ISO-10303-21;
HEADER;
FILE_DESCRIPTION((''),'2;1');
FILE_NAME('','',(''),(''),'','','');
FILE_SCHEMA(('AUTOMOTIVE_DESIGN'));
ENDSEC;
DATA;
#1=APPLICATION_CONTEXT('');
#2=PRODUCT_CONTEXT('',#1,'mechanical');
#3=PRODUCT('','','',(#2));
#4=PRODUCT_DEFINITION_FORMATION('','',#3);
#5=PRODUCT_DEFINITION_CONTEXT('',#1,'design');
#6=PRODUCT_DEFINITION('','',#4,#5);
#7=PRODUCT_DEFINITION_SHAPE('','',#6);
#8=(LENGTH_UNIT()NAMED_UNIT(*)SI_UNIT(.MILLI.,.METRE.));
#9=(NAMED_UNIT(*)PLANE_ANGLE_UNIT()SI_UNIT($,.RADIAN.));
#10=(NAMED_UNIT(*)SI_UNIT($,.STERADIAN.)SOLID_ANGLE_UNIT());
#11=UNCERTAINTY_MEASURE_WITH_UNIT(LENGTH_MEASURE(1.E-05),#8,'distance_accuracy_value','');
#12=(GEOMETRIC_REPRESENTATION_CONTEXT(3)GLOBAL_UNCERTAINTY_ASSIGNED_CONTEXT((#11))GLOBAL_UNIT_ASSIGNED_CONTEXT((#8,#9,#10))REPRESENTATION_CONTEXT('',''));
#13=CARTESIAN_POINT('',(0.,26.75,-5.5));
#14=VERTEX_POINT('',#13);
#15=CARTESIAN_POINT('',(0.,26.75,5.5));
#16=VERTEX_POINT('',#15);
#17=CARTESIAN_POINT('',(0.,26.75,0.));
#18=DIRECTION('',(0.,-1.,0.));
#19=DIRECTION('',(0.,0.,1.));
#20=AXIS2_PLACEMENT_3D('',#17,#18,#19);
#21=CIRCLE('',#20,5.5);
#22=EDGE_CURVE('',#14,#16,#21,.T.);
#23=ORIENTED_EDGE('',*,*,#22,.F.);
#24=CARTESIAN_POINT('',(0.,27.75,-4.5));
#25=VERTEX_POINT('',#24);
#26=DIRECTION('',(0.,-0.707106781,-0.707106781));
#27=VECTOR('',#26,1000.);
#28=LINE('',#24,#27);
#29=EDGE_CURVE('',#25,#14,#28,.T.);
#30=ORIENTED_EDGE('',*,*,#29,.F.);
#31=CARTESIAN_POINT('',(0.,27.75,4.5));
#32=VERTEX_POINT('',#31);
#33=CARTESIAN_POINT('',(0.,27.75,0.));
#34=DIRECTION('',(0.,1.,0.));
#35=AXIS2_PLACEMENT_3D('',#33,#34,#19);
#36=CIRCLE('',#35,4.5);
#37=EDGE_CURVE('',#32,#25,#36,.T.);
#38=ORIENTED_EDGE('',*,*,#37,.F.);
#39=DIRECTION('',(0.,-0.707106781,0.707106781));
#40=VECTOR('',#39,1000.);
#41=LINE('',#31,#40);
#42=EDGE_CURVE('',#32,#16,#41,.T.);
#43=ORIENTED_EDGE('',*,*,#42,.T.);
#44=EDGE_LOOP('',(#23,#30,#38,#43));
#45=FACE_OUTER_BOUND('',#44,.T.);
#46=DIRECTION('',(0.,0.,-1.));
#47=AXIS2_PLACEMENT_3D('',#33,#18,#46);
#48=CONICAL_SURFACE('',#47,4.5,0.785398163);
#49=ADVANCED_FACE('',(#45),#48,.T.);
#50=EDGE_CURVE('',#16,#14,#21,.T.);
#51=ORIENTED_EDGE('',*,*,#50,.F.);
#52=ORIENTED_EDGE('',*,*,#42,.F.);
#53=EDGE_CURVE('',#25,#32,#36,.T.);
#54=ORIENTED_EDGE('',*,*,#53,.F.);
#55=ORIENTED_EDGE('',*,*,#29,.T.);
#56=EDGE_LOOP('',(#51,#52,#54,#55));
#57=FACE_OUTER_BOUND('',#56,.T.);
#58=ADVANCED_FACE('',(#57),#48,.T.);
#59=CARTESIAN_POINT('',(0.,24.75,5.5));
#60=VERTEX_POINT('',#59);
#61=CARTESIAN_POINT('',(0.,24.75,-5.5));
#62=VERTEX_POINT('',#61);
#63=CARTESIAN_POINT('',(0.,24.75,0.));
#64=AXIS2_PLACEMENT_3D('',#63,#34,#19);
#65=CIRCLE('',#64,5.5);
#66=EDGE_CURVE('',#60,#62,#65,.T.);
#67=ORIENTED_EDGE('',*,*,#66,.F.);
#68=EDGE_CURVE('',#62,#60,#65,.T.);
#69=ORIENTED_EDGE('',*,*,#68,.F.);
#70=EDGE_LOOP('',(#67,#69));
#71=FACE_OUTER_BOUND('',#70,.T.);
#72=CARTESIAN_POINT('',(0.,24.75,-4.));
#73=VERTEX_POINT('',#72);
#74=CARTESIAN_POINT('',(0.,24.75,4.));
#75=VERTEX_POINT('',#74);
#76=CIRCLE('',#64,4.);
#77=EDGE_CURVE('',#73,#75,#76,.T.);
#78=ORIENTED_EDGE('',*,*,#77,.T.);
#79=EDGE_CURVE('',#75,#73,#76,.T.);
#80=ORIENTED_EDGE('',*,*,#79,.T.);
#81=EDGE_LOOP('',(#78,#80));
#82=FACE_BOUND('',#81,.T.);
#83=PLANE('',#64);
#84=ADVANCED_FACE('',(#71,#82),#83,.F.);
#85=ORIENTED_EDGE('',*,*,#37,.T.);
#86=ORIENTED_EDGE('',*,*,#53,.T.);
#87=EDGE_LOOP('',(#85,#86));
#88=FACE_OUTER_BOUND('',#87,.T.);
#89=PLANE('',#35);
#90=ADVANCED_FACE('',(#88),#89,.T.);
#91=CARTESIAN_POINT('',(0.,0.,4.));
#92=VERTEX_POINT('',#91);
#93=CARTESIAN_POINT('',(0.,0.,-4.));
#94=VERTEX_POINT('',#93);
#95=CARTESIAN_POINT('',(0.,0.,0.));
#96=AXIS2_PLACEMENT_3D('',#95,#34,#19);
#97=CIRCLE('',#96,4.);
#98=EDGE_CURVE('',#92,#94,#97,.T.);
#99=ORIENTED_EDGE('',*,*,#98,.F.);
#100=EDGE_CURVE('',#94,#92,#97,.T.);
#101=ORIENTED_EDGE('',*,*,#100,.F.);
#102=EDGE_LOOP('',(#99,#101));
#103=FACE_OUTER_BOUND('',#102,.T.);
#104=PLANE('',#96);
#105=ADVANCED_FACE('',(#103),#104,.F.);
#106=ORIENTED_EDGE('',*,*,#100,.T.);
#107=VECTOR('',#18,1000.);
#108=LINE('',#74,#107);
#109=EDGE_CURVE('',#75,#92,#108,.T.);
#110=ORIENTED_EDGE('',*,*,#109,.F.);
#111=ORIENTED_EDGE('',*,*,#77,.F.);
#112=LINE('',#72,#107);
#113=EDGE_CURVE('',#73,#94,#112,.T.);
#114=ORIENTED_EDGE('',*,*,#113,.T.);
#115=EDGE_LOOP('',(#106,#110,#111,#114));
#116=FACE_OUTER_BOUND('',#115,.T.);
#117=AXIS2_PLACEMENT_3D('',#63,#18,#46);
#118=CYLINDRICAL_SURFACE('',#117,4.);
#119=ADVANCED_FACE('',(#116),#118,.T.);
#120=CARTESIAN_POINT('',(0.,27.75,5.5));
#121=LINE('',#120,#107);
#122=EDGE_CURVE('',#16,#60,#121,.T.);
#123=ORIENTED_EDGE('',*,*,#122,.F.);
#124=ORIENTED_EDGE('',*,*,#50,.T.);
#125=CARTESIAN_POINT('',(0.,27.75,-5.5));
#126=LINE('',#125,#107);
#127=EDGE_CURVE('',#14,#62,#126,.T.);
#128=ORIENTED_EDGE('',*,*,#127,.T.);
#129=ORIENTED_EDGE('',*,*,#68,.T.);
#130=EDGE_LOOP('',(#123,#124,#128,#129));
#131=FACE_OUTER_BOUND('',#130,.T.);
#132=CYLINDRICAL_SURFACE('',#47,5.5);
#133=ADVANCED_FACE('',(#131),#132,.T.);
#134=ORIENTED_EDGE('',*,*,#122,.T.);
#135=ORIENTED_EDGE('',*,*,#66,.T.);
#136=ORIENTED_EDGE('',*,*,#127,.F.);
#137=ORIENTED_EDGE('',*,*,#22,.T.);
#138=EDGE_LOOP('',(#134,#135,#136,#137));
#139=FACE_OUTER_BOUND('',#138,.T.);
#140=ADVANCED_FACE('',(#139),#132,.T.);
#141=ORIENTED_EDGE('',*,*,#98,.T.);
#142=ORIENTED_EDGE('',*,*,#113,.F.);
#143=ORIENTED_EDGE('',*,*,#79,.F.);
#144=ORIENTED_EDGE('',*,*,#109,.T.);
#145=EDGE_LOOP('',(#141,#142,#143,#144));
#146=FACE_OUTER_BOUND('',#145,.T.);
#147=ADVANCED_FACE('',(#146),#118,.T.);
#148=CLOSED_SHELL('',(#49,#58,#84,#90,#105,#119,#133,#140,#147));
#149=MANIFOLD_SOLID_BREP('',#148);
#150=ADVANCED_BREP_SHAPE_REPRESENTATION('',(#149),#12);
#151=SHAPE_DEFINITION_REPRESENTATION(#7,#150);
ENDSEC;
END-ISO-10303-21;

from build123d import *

# Parameters (mm, degrees)
SHANK_PROFILE_8_R      = 4
SHANK_8_DEPTH          = 24.75
HEAD_PROFILE_14_R      = 5.5
HEAD_14_DEPTH          = 3
HEAD_CHAMFER_1X45_SIZE = 1


with BuildPart() as part:
    # Shank Profile Ø8 → Shank Ø8 (new body)
    with BuildSketch(Plane(origin=(0, 0, 0), x_dir=(1, 0, 0), z_dir=(0, 1, 0))):
        with Locations(Location((0, 0, 0), (0, 0, 270))):
            Circle(SHANK_PROFILE_8_R)
    extrude(amount=SHANK_8_DEPTH)

    # Head Profile Ø14 → Head Ø14 (add)
    with BuildSketch(Plane(origin=(0, 24.75, 0), x_dir=(1, 0, 0), z_dir=(0, 1, 0))):
        with Locations(Location((0, 0, 0), (0, 0, 270))):
            Circle(HEAD_PROFILE_14_R)
    extrude(amount=HEAD_14_DEPTH)

    # Head Chamfer 1x45°
    head_chamfer_1x45_edges = [part.edges().sort_by_distance(p)[0] for p in [
        (0, 27.75, -5.5),
    ]]
    chamfer(head_chamfer_1x45_edges, length=HEAD_CHAMFER_1X45_SIZE)


solid = part.part
